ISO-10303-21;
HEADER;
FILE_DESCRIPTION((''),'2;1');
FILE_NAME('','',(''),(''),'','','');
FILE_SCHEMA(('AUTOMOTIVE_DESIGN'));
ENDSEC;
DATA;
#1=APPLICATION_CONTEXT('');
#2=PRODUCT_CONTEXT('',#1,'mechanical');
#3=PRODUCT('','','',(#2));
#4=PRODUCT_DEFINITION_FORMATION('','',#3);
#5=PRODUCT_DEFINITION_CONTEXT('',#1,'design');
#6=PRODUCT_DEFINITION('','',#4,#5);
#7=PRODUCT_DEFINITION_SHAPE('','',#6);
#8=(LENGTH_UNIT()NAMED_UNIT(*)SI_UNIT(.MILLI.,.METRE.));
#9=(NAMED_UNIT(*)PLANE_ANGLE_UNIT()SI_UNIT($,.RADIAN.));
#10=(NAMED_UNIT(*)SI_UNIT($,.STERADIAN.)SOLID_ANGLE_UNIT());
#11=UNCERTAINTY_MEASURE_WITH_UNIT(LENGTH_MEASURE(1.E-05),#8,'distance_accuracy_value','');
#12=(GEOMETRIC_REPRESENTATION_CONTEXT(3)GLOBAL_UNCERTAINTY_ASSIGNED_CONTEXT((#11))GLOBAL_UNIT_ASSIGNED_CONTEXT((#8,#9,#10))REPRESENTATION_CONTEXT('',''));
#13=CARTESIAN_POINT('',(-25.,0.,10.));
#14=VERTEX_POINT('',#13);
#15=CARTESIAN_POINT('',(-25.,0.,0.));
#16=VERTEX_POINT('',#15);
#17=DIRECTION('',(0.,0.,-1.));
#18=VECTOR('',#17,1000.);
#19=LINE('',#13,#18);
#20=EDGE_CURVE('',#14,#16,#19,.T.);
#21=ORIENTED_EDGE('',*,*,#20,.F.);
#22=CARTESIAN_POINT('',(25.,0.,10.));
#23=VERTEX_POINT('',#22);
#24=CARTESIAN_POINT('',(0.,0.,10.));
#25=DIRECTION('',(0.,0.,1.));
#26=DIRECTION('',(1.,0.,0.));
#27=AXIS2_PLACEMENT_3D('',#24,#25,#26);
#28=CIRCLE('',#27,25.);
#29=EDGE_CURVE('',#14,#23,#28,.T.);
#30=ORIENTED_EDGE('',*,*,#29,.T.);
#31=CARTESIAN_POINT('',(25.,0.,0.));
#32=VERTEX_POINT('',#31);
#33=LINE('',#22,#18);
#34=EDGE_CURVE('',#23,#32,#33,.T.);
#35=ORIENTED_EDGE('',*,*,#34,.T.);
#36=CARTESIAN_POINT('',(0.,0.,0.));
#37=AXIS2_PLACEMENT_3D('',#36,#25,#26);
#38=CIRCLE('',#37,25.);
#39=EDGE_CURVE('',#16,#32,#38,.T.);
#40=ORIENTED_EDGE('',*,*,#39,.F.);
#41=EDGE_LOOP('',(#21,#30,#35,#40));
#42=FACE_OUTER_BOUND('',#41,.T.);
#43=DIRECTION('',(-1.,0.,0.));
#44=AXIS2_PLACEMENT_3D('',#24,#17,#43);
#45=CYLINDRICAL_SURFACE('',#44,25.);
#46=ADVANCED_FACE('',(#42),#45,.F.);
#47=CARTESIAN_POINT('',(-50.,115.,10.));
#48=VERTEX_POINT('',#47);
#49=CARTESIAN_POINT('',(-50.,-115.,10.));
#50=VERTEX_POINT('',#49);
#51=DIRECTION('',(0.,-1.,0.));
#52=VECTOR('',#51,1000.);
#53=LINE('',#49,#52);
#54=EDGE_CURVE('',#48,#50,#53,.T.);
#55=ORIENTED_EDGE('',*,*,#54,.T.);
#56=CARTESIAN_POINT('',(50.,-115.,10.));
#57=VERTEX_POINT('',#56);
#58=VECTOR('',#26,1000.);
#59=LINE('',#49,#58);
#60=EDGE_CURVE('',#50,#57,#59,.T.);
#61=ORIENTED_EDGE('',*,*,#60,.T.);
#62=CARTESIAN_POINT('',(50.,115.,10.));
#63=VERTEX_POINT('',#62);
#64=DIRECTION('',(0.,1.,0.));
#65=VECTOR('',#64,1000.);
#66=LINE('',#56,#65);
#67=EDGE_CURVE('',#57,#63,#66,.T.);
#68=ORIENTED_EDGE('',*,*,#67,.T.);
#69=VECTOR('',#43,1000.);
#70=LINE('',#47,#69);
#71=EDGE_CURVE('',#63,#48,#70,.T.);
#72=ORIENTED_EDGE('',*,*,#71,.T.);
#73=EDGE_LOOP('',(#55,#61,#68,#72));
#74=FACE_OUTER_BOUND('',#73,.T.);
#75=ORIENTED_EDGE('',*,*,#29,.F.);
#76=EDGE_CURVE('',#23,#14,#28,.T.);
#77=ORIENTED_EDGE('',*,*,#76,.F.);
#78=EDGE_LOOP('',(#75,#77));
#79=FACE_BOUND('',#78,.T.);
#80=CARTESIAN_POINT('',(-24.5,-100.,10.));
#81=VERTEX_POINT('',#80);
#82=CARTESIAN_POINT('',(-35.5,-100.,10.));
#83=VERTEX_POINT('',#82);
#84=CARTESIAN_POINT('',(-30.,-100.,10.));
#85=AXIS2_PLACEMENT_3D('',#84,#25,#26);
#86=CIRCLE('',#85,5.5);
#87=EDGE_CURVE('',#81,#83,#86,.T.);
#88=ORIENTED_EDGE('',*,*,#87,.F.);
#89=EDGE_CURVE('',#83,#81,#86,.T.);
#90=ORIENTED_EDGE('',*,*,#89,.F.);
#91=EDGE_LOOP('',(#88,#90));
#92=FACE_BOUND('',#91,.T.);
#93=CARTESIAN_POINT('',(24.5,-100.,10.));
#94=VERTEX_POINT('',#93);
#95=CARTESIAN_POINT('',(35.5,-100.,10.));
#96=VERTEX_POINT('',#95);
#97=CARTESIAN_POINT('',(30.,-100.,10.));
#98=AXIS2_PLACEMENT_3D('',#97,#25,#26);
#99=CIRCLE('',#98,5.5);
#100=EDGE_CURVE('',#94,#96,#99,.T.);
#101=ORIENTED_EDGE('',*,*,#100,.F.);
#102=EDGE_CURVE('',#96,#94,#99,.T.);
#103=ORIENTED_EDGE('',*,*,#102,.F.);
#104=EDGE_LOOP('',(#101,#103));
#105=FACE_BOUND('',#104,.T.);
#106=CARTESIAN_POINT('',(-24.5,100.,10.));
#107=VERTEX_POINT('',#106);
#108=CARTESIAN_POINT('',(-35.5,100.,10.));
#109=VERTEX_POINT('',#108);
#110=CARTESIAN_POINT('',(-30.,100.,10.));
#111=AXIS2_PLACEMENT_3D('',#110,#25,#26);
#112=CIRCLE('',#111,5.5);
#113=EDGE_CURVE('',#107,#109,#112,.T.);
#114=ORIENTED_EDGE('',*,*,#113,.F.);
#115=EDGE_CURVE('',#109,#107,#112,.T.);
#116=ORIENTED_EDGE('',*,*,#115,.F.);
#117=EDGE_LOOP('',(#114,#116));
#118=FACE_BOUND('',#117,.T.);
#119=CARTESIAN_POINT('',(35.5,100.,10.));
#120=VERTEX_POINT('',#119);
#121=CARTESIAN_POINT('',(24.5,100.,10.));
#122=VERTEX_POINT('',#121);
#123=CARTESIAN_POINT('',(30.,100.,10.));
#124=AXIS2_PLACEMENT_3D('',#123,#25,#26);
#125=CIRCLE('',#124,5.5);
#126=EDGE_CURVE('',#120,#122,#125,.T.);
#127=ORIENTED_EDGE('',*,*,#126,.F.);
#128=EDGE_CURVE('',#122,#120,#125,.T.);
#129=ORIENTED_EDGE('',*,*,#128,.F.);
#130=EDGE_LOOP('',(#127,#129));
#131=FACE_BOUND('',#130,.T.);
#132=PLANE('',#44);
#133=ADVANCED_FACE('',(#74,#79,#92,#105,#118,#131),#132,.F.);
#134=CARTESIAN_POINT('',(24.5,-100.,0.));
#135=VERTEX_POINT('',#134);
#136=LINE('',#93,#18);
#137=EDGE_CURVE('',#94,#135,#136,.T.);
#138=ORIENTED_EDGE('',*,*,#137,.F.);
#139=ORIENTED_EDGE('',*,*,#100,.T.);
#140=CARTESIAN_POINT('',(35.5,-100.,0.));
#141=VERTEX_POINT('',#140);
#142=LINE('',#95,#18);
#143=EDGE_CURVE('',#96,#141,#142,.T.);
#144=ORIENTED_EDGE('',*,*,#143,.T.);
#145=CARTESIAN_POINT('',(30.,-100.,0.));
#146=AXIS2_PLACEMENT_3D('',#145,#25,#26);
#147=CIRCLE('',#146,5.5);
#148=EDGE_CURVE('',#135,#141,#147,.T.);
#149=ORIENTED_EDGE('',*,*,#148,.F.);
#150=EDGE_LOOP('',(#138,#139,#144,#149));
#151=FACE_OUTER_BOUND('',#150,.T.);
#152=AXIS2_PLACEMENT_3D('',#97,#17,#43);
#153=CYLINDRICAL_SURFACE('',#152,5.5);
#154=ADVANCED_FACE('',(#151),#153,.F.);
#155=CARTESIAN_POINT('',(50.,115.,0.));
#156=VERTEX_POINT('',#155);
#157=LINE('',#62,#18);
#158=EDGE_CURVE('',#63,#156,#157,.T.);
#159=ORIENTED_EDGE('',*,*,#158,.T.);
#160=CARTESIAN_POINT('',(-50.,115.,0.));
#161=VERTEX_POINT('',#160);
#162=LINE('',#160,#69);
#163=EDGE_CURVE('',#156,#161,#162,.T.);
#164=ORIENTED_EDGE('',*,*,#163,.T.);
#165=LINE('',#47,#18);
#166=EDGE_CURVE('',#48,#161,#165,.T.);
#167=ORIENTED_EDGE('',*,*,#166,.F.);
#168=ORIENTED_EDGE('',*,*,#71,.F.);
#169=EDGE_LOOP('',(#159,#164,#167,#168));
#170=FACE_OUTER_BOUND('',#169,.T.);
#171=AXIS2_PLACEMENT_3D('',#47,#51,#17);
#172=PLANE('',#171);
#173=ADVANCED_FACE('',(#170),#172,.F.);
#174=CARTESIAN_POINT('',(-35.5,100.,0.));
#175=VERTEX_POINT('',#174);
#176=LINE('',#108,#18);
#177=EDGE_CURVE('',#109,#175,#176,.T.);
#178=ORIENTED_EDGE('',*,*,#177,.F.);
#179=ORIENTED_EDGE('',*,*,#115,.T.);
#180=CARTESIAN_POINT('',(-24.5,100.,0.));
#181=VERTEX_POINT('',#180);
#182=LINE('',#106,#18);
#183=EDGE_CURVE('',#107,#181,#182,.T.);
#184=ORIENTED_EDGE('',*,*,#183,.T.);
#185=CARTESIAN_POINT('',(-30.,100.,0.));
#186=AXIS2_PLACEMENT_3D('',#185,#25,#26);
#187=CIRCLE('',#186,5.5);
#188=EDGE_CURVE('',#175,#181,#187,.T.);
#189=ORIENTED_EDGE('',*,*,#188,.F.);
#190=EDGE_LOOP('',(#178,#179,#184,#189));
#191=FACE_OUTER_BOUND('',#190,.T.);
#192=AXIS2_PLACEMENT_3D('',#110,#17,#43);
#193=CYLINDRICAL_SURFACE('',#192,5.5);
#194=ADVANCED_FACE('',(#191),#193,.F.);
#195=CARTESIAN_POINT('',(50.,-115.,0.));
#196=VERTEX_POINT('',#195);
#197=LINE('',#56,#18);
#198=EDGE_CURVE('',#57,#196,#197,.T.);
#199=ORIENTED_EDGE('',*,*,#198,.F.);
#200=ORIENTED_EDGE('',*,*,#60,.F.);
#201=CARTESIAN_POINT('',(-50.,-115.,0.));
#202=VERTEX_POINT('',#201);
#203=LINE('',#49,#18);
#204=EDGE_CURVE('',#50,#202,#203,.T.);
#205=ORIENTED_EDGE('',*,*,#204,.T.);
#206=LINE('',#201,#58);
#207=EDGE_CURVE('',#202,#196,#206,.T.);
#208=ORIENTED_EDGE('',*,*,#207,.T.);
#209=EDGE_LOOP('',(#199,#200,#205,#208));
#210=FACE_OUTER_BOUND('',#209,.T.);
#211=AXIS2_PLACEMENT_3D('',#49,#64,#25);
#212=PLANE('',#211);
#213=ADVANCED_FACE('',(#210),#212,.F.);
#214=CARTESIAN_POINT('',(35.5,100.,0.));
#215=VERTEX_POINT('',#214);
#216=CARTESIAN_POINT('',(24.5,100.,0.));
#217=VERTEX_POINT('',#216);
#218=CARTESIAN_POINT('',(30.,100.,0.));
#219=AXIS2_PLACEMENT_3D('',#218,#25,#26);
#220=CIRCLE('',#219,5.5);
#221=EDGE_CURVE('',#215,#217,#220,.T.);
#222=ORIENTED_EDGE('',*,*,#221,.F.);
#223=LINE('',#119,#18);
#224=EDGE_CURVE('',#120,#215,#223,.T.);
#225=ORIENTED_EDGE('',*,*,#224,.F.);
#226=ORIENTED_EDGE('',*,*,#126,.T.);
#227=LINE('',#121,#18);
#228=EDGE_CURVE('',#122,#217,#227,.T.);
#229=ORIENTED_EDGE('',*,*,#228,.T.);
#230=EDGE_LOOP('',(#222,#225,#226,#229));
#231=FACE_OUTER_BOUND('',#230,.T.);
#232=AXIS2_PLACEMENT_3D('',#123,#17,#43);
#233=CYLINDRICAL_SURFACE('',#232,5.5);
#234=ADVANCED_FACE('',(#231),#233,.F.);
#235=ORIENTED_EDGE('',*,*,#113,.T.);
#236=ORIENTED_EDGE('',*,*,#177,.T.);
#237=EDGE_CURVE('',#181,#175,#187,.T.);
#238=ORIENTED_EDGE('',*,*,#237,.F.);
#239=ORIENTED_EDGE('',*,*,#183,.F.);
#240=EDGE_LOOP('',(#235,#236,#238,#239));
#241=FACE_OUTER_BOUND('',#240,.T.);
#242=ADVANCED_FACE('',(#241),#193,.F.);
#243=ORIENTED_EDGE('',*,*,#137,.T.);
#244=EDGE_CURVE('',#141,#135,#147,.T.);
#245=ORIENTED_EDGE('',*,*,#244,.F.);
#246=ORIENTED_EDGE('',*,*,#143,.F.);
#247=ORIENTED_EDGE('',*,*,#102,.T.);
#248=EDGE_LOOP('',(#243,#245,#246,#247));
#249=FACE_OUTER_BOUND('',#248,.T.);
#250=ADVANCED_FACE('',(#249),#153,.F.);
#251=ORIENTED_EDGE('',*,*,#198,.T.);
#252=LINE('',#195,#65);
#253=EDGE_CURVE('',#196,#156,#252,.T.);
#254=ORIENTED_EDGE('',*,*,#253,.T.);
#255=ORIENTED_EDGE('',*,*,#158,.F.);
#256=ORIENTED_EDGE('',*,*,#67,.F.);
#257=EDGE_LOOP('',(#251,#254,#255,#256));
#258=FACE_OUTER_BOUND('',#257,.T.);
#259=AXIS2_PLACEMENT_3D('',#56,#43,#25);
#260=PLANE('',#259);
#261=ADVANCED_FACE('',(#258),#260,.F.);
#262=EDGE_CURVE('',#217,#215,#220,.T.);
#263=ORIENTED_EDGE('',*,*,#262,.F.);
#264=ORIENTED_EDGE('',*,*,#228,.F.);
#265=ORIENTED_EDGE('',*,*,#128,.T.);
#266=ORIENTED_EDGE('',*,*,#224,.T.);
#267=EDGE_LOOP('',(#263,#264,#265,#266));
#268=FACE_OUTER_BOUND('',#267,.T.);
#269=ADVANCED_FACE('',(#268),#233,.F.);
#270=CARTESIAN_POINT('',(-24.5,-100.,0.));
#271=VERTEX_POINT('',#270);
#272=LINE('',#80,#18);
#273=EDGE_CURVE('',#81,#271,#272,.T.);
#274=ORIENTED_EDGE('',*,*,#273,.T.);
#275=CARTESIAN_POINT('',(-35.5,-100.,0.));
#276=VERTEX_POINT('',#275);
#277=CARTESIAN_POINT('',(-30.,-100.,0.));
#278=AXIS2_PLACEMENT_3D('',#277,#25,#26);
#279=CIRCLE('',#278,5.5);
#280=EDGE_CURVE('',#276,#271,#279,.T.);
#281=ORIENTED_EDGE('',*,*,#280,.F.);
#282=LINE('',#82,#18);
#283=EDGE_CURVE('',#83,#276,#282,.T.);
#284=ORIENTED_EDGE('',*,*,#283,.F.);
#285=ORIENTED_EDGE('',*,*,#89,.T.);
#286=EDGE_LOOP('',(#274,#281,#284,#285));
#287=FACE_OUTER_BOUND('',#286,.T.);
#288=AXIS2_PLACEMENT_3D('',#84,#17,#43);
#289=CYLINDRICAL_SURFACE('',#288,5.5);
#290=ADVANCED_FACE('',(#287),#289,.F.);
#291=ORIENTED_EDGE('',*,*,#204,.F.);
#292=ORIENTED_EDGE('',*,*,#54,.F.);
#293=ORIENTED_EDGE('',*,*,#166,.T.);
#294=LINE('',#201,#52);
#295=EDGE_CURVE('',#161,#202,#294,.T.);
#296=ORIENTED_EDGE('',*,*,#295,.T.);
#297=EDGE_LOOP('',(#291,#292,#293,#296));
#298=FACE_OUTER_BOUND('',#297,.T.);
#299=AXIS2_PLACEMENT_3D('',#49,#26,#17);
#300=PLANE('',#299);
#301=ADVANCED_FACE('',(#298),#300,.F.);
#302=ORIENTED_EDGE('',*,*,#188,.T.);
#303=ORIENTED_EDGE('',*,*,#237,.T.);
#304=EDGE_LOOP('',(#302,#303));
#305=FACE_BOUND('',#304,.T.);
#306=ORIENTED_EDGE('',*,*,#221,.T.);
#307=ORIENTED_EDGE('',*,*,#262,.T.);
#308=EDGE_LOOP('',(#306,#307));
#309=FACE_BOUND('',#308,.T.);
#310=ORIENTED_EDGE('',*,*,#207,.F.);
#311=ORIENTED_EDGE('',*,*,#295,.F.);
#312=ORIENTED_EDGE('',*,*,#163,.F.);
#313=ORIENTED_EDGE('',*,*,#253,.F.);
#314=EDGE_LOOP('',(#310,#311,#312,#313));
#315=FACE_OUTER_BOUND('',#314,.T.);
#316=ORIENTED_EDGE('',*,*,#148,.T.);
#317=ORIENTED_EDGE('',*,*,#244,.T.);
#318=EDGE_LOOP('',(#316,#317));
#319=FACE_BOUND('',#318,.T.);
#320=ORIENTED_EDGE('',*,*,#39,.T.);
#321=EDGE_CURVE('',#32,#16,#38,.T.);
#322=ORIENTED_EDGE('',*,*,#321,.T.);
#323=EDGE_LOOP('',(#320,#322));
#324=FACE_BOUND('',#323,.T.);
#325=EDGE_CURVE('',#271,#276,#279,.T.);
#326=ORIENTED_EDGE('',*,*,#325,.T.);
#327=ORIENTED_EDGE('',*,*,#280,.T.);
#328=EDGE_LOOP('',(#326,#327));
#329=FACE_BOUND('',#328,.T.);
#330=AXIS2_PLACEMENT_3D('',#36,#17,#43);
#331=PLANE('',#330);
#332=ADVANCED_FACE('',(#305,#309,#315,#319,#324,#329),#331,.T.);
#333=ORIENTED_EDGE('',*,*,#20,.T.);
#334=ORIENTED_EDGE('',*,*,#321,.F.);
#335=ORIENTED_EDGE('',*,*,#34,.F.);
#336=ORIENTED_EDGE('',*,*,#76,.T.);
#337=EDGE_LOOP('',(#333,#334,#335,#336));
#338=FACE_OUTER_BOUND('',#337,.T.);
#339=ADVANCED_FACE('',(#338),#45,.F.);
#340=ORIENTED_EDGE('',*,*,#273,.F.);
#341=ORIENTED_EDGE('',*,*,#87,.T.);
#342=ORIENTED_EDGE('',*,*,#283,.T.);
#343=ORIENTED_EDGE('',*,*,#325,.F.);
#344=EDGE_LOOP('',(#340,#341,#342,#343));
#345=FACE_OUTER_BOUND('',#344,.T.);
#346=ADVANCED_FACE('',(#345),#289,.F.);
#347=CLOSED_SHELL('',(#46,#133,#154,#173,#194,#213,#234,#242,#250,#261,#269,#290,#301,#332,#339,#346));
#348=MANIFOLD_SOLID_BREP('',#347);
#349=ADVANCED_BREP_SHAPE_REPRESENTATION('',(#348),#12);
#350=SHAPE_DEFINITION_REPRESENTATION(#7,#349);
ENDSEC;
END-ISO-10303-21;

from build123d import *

# Parameters (mm, degrees)
SKETCH_1_W          = 100
SKETCH_1_H          = 230
SKETCH_1_R          = 25
SKETCH_1_R_2        = 5.5
BOSS_EXTRUDE1_DEPTH = 10


with BuildPart() as part:
    # Sketch 1 → Boss-Extrude1 (new body)
    with BuildSketch(Plane.XY):
        Rectangle(SKETCH_1_W, SKETCH_1_H)
        Circle(SKETCH_1_R, mode=Mode.SUBTRACT)
        with Locations((-30, 100)):
            Circle(SKETCH_1_R_2, mode=Mode.SUBTRACT)
        with Locations((30, 100)):
            Circle(SKETCH_1_R_2, mode=Mode.SUBTRACT)
        with Locations((30, -100)):
            Circle(SKETCH_1_R_2, mode=Mode.SUBTRACT)
        with Locations((-30, -100)):
            Circle(SKETCH_1_R_2, mode=Mode.SUBTRACT)
    extrude(amount=BOSS_EXTRUDE1_DEPTH)


solid = part.part
